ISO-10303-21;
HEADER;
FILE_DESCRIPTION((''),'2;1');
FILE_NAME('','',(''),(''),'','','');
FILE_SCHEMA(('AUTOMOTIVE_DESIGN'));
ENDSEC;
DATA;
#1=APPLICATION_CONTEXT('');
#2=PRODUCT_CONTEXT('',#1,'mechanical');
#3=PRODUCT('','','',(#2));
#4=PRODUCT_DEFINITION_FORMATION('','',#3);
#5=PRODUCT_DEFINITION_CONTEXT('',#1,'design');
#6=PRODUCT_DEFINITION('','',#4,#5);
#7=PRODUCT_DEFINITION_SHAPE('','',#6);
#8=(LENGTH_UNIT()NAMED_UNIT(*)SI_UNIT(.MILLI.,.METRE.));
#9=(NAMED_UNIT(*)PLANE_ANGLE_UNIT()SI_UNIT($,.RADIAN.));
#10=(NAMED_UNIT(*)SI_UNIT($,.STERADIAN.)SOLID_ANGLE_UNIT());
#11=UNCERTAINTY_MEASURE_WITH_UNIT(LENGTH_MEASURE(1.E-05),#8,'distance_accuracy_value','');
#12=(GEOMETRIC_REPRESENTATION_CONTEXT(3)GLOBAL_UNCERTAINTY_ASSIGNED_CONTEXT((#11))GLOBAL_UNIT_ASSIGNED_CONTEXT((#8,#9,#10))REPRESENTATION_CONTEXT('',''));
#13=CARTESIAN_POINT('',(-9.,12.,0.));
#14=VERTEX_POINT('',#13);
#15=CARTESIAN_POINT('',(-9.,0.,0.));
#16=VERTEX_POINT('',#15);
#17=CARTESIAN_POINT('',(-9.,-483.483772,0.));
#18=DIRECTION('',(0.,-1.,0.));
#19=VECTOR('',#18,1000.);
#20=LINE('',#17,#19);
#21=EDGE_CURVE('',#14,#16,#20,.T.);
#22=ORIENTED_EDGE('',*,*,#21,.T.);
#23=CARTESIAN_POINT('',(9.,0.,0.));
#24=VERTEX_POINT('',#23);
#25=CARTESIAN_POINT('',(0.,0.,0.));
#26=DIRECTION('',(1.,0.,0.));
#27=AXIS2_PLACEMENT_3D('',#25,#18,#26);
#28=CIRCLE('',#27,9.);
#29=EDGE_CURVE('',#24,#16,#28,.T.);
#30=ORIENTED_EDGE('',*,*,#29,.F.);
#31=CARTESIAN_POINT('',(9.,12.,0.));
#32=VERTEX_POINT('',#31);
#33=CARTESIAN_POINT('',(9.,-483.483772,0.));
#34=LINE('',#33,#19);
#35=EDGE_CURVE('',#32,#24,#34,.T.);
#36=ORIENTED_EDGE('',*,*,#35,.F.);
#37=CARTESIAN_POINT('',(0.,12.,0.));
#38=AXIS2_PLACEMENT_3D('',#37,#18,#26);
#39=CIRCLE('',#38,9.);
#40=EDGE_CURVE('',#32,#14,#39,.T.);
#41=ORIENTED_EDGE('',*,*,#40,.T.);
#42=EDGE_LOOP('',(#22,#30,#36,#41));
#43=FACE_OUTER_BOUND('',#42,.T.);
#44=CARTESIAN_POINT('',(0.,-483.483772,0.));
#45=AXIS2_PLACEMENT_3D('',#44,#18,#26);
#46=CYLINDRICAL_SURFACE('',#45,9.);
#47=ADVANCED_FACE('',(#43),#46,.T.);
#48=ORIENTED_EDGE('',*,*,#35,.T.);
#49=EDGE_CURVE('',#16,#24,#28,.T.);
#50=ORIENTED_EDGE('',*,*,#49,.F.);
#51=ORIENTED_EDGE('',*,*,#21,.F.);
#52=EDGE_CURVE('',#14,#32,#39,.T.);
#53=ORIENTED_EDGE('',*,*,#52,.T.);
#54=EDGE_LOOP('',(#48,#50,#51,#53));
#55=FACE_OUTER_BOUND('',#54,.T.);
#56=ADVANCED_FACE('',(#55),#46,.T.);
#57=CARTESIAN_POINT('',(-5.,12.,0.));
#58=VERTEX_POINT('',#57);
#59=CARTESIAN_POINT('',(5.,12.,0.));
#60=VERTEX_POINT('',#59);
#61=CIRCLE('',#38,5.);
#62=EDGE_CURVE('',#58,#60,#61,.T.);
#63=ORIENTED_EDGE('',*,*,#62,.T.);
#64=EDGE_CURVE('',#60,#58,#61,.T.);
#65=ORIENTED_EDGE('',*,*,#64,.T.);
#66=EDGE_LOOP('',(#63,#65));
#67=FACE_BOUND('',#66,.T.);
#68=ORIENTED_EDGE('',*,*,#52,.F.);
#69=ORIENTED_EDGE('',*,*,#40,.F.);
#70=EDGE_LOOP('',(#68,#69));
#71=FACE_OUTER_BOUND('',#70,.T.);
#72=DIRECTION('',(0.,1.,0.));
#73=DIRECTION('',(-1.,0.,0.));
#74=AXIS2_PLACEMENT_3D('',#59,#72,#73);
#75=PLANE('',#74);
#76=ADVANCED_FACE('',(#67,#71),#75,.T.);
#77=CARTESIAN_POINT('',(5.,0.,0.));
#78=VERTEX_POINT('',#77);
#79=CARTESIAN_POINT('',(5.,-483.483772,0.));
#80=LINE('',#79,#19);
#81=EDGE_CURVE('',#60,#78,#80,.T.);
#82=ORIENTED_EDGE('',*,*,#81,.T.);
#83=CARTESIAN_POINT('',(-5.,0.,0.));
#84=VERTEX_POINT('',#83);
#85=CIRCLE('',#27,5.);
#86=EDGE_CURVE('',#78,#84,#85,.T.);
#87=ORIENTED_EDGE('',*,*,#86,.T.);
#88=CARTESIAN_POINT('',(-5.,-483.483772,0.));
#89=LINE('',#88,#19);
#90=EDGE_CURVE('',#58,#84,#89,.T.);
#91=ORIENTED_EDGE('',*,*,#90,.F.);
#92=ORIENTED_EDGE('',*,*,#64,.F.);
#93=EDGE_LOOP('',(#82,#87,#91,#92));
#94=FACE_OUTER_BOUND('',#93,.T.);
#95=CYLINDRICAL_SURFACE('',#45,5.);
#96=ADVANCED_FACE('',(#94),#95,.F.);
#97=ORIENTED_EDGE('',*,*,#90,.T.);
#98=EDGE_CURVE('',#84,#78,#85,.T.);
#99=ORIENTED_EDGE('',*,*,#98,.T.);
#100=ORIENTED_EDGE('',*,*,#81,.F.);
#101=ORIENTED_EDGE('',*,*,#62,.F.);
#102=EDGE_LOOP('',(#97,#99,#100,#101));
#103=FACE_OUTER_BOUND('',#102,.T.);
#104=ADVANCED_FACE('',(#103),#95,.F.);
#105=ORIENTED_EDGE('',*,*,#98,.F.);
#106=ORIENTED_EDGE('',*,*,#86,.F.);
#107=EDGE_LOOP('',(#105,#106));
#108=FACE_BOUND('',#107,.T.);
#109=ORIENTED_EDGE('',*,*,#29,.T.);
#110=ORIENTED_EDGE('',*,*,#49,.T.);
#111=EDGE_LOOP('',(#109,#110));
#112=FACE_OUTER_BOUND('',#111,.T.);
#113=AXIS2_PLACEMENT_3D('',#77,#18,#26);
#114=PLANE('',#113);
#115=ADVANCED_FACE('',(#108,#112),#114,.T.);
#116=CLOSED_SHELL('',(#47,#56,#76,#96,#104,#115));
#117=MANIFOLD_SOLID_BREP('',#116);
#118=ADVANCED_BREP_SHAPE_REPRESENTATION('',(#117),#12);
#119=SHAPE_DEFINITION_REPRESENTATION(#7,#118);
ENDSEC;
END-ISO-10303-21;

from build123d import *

# Parameters (mm, degrees)
SKETCH1_W = 4
SKETCH1_H = 12


with BuildPart() as part:
    # Sketch1 → Revolve1 (revolve)
    with BuildSketch(Plane.XY):
        with Locations((7, 6)):
            Rectangle(SKETCH1_W, SKETCH1_H)
    revolve(axis=Axis((0, -483.483771846, 0), (0, 1, 0)))


solid = part.part
